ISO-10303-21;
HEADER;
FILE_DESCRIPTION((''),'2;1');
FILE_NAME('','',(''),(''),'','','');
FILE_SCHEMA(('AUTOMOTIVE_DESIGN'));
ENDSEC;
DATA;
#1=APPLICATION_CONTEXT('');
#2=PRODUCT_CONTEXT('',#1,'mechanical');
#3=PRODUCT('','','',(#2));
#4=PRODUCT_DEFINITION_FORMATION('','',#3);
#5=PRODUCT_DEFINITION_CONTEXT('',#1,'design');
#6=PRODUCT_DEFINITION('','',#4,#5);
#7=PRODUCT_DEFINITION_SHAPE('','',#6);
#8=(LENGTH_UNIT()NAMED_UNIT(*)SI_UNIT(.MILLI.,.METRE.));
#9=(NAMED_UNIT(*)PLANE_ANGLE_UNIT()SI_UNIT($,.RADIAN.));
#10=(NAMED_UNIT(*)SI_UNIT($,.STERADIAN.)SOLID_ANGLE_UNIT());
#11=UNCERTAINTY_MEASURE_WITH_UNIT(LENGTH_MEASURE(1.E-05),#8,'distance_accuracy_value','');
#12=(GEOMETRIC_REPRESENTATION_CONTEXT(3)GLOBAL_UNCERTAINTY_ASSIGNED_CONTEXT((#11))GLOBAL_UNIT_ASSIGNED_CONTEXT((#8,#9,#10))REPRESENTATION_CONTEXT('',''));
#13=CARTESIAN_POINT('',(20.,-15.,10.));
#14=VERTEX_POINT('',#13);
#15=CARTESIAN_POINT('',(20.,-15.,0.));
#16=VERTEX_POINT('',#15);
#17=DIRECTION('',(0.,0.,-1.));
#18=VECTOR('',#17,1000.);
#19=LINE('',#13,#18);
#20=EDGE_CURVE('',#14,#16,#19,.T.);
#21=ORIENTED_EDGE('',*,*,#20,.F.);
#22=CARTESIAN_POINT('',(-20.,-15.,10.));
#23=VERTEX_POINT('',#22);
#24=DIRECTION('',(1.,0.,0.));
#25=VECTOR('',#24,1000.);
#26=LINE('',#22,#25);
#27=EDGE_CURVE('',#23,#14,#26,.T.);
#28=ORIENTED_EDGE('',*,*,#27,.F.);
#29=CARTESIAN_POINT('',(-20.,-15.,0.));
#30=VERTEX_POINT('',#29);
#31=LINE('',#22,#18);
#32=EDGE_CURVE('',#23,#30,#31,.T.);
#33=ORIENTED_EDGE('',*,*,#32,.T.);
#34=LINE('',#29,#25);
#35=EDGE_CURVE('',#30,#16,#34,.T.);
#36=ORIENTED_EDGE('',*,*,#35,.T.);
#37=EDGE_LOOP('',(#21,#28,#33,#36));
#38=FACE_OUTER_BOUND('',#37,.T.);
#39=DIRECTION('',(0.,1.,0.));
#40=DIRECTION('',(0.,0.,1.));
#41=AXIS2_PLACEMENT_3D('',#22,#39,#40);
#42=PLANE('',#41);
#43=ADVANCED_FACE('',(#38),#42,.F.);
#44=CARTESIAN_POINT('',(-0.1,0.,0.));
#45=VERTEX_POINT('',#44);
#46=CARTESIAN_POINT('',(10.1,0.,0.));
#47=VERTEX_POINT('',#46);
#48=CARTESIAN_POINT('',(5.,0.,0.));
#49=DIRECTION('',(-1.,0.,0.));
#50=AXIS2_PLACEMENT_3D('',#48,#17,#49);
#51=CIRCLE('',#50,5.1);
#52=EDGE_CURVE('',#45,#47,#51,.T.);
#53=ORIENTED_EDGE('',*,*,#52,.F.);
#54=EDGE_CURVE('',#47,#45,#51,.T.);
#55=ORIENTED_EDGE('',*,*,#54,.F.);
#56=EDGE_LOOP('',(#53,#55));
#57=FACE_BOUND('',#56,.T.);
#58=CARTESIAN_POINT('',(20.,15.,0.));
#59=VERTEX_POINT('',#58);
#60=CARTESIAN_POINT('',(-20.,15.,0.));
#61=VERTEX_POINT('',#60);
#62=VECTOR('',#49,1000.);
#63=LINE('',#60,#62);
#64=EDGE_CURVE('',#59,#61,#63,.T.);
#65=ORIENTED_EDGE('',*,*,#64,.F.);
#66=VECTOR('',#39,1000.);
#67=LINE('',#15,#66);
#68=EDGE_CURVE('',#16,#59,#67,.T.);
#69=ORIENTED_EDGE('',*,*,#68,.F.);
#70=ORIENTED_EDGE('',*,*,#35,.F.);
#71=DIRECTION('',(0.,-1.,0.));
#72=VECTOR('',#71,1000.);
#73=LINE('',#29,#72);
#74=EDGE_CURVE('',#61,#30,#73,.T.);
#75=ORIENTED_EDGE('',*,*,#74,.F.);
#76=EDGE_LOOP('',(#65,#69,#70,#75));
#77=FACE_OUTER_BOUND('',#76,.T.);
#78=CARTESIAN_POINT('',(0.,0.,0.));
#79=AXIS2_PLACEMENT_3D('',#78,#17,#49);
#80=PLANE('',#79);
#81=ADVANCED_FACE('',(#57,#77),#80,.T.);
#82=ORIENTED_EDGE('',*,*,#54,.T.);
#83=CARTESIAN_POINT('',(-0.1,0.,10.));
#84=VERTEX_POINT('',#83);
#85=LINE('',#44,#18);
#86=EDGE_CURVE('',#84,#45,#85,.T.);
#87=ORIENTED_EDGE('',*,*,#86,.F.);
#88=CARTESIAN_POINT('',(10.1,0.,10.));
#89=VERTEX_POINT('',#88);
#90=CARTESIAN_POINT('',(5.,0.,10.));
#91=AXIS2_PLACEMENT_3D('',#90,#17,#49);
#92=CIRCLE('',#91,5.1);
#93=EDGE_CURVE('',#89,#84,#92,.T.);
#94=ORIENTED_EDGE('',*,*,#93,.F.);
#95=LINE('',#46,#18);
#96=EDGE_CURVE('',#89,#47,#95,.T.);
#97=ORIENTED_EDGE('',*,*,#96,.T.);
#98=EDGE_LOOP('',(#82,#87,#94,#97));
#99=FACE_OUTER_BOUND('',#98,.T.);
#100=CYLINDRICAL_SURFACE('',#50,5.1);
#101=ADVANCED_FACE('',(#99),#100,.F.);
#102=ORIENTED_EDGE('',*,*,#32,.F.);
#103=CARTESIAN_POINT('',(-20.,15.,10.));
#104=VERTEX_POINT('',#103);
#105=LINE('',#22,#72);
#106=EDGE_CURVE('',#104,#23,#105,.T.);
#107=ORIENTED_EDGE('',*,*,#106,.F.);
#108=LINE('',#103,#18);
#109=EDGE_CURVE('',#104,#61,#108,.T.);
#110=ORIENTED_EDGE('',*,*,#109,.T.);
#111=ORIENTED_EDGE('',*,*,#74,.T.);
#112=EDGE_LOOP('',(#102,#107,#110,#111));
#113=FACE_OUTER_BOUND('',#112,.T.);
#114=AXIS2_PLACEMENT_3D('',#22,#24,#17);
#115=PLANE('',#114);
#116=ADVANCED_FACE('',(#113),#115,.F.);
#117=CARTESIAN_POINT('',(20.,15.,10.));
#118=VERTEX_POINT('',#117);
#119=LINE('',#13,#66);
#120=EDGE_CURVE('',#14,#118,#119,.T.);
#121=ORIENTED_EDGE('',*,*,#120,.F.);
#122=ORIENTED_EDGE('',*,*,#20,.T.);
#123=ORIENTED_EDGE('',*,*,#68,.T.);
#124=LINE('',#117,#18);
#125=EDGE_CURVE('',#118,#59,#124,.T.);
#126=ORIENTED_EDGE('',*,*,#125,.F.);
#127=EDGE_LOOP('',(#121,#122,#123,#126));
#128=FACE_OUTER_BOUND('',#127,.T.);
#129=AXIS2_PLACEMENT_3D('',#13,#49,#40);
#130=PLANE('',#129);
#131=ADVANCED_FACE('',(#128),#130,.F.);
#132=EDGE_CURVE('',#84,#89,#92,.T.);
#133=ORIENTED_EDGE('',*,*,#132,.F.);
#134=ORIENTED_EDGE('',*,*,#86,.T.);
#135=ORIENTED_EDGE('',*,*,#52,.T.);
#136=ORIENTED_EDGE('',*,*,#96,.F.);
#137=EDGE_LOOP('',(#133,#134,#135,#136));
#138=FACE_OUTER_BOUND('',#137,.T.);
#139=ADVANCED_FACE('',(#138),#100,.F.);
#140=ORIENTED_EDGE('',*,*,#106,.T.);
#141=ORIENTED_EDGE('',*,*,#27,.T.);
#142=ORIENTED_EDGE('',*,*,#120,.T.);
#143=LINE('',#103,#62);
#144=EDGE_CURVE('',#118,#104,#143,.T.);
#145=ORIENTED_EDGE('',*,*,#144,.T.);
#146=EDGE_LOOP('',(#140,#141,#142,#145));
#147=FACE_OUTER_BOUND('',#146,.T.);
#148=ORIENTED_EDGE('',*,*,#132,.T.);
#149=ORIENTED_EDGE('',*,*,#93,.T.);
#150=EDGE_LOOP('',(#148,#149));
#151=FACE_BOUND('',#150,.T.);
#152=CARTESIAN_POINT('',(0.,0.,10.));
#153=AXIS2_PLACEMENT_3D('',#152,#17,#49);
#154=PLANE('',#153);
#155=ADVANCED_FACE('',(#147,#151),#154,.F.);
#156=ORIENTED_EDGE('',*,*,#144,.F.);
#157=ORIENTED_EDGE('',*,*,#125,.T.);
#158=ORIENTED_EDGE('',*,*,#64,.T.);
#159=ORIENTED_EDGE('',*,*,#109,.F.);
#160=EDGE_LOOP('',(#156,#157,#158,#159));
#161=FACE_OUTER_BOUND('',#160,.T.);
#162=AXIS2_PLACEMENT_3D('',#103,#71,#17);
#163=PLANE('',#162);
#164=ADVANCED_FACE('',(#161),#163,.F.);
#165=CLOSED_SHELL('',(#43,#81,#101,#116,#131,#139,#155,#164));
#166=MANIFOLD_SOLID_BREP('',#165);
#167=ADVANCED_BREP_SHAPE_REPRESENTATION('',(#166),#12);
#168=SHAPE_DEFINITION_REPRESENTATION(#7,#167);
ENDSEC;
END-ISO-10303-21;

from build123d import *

# Parameters (mm, degrees)
SKETCH1_W           = 40
SKETCH1_H           = 30
SKETCH1_R           = 5
BOSS_EXTRUDE1_DEPTH = 10
M12_TAPPED_HOLE1_D  = 10.2


with BuildPart() as part:
    # Sketch1 → Boss-Extrude1 (new body)
    with BuildSketch(Plane.XY):
        Rectangle(SKETCH1_W, SKETCH1_H)
        with Locations((5, 0)):
            Circle(SKETCH1_R, mode=Mode.SUBTRACT)
    extrude(amount=BOSS_EXTRUDE1_DEPTH)

    # M12 Tapped Hole1 (through all)
    with Locations(Plane(origin=(5, 0, 0), x_dir=(-1, 0, 0), z_dir=(0, 0, -1))):
        with Locations((0, 0)):
            Hole(M12_TAPPED_HOLE1_D / 2)


solid = part.part
